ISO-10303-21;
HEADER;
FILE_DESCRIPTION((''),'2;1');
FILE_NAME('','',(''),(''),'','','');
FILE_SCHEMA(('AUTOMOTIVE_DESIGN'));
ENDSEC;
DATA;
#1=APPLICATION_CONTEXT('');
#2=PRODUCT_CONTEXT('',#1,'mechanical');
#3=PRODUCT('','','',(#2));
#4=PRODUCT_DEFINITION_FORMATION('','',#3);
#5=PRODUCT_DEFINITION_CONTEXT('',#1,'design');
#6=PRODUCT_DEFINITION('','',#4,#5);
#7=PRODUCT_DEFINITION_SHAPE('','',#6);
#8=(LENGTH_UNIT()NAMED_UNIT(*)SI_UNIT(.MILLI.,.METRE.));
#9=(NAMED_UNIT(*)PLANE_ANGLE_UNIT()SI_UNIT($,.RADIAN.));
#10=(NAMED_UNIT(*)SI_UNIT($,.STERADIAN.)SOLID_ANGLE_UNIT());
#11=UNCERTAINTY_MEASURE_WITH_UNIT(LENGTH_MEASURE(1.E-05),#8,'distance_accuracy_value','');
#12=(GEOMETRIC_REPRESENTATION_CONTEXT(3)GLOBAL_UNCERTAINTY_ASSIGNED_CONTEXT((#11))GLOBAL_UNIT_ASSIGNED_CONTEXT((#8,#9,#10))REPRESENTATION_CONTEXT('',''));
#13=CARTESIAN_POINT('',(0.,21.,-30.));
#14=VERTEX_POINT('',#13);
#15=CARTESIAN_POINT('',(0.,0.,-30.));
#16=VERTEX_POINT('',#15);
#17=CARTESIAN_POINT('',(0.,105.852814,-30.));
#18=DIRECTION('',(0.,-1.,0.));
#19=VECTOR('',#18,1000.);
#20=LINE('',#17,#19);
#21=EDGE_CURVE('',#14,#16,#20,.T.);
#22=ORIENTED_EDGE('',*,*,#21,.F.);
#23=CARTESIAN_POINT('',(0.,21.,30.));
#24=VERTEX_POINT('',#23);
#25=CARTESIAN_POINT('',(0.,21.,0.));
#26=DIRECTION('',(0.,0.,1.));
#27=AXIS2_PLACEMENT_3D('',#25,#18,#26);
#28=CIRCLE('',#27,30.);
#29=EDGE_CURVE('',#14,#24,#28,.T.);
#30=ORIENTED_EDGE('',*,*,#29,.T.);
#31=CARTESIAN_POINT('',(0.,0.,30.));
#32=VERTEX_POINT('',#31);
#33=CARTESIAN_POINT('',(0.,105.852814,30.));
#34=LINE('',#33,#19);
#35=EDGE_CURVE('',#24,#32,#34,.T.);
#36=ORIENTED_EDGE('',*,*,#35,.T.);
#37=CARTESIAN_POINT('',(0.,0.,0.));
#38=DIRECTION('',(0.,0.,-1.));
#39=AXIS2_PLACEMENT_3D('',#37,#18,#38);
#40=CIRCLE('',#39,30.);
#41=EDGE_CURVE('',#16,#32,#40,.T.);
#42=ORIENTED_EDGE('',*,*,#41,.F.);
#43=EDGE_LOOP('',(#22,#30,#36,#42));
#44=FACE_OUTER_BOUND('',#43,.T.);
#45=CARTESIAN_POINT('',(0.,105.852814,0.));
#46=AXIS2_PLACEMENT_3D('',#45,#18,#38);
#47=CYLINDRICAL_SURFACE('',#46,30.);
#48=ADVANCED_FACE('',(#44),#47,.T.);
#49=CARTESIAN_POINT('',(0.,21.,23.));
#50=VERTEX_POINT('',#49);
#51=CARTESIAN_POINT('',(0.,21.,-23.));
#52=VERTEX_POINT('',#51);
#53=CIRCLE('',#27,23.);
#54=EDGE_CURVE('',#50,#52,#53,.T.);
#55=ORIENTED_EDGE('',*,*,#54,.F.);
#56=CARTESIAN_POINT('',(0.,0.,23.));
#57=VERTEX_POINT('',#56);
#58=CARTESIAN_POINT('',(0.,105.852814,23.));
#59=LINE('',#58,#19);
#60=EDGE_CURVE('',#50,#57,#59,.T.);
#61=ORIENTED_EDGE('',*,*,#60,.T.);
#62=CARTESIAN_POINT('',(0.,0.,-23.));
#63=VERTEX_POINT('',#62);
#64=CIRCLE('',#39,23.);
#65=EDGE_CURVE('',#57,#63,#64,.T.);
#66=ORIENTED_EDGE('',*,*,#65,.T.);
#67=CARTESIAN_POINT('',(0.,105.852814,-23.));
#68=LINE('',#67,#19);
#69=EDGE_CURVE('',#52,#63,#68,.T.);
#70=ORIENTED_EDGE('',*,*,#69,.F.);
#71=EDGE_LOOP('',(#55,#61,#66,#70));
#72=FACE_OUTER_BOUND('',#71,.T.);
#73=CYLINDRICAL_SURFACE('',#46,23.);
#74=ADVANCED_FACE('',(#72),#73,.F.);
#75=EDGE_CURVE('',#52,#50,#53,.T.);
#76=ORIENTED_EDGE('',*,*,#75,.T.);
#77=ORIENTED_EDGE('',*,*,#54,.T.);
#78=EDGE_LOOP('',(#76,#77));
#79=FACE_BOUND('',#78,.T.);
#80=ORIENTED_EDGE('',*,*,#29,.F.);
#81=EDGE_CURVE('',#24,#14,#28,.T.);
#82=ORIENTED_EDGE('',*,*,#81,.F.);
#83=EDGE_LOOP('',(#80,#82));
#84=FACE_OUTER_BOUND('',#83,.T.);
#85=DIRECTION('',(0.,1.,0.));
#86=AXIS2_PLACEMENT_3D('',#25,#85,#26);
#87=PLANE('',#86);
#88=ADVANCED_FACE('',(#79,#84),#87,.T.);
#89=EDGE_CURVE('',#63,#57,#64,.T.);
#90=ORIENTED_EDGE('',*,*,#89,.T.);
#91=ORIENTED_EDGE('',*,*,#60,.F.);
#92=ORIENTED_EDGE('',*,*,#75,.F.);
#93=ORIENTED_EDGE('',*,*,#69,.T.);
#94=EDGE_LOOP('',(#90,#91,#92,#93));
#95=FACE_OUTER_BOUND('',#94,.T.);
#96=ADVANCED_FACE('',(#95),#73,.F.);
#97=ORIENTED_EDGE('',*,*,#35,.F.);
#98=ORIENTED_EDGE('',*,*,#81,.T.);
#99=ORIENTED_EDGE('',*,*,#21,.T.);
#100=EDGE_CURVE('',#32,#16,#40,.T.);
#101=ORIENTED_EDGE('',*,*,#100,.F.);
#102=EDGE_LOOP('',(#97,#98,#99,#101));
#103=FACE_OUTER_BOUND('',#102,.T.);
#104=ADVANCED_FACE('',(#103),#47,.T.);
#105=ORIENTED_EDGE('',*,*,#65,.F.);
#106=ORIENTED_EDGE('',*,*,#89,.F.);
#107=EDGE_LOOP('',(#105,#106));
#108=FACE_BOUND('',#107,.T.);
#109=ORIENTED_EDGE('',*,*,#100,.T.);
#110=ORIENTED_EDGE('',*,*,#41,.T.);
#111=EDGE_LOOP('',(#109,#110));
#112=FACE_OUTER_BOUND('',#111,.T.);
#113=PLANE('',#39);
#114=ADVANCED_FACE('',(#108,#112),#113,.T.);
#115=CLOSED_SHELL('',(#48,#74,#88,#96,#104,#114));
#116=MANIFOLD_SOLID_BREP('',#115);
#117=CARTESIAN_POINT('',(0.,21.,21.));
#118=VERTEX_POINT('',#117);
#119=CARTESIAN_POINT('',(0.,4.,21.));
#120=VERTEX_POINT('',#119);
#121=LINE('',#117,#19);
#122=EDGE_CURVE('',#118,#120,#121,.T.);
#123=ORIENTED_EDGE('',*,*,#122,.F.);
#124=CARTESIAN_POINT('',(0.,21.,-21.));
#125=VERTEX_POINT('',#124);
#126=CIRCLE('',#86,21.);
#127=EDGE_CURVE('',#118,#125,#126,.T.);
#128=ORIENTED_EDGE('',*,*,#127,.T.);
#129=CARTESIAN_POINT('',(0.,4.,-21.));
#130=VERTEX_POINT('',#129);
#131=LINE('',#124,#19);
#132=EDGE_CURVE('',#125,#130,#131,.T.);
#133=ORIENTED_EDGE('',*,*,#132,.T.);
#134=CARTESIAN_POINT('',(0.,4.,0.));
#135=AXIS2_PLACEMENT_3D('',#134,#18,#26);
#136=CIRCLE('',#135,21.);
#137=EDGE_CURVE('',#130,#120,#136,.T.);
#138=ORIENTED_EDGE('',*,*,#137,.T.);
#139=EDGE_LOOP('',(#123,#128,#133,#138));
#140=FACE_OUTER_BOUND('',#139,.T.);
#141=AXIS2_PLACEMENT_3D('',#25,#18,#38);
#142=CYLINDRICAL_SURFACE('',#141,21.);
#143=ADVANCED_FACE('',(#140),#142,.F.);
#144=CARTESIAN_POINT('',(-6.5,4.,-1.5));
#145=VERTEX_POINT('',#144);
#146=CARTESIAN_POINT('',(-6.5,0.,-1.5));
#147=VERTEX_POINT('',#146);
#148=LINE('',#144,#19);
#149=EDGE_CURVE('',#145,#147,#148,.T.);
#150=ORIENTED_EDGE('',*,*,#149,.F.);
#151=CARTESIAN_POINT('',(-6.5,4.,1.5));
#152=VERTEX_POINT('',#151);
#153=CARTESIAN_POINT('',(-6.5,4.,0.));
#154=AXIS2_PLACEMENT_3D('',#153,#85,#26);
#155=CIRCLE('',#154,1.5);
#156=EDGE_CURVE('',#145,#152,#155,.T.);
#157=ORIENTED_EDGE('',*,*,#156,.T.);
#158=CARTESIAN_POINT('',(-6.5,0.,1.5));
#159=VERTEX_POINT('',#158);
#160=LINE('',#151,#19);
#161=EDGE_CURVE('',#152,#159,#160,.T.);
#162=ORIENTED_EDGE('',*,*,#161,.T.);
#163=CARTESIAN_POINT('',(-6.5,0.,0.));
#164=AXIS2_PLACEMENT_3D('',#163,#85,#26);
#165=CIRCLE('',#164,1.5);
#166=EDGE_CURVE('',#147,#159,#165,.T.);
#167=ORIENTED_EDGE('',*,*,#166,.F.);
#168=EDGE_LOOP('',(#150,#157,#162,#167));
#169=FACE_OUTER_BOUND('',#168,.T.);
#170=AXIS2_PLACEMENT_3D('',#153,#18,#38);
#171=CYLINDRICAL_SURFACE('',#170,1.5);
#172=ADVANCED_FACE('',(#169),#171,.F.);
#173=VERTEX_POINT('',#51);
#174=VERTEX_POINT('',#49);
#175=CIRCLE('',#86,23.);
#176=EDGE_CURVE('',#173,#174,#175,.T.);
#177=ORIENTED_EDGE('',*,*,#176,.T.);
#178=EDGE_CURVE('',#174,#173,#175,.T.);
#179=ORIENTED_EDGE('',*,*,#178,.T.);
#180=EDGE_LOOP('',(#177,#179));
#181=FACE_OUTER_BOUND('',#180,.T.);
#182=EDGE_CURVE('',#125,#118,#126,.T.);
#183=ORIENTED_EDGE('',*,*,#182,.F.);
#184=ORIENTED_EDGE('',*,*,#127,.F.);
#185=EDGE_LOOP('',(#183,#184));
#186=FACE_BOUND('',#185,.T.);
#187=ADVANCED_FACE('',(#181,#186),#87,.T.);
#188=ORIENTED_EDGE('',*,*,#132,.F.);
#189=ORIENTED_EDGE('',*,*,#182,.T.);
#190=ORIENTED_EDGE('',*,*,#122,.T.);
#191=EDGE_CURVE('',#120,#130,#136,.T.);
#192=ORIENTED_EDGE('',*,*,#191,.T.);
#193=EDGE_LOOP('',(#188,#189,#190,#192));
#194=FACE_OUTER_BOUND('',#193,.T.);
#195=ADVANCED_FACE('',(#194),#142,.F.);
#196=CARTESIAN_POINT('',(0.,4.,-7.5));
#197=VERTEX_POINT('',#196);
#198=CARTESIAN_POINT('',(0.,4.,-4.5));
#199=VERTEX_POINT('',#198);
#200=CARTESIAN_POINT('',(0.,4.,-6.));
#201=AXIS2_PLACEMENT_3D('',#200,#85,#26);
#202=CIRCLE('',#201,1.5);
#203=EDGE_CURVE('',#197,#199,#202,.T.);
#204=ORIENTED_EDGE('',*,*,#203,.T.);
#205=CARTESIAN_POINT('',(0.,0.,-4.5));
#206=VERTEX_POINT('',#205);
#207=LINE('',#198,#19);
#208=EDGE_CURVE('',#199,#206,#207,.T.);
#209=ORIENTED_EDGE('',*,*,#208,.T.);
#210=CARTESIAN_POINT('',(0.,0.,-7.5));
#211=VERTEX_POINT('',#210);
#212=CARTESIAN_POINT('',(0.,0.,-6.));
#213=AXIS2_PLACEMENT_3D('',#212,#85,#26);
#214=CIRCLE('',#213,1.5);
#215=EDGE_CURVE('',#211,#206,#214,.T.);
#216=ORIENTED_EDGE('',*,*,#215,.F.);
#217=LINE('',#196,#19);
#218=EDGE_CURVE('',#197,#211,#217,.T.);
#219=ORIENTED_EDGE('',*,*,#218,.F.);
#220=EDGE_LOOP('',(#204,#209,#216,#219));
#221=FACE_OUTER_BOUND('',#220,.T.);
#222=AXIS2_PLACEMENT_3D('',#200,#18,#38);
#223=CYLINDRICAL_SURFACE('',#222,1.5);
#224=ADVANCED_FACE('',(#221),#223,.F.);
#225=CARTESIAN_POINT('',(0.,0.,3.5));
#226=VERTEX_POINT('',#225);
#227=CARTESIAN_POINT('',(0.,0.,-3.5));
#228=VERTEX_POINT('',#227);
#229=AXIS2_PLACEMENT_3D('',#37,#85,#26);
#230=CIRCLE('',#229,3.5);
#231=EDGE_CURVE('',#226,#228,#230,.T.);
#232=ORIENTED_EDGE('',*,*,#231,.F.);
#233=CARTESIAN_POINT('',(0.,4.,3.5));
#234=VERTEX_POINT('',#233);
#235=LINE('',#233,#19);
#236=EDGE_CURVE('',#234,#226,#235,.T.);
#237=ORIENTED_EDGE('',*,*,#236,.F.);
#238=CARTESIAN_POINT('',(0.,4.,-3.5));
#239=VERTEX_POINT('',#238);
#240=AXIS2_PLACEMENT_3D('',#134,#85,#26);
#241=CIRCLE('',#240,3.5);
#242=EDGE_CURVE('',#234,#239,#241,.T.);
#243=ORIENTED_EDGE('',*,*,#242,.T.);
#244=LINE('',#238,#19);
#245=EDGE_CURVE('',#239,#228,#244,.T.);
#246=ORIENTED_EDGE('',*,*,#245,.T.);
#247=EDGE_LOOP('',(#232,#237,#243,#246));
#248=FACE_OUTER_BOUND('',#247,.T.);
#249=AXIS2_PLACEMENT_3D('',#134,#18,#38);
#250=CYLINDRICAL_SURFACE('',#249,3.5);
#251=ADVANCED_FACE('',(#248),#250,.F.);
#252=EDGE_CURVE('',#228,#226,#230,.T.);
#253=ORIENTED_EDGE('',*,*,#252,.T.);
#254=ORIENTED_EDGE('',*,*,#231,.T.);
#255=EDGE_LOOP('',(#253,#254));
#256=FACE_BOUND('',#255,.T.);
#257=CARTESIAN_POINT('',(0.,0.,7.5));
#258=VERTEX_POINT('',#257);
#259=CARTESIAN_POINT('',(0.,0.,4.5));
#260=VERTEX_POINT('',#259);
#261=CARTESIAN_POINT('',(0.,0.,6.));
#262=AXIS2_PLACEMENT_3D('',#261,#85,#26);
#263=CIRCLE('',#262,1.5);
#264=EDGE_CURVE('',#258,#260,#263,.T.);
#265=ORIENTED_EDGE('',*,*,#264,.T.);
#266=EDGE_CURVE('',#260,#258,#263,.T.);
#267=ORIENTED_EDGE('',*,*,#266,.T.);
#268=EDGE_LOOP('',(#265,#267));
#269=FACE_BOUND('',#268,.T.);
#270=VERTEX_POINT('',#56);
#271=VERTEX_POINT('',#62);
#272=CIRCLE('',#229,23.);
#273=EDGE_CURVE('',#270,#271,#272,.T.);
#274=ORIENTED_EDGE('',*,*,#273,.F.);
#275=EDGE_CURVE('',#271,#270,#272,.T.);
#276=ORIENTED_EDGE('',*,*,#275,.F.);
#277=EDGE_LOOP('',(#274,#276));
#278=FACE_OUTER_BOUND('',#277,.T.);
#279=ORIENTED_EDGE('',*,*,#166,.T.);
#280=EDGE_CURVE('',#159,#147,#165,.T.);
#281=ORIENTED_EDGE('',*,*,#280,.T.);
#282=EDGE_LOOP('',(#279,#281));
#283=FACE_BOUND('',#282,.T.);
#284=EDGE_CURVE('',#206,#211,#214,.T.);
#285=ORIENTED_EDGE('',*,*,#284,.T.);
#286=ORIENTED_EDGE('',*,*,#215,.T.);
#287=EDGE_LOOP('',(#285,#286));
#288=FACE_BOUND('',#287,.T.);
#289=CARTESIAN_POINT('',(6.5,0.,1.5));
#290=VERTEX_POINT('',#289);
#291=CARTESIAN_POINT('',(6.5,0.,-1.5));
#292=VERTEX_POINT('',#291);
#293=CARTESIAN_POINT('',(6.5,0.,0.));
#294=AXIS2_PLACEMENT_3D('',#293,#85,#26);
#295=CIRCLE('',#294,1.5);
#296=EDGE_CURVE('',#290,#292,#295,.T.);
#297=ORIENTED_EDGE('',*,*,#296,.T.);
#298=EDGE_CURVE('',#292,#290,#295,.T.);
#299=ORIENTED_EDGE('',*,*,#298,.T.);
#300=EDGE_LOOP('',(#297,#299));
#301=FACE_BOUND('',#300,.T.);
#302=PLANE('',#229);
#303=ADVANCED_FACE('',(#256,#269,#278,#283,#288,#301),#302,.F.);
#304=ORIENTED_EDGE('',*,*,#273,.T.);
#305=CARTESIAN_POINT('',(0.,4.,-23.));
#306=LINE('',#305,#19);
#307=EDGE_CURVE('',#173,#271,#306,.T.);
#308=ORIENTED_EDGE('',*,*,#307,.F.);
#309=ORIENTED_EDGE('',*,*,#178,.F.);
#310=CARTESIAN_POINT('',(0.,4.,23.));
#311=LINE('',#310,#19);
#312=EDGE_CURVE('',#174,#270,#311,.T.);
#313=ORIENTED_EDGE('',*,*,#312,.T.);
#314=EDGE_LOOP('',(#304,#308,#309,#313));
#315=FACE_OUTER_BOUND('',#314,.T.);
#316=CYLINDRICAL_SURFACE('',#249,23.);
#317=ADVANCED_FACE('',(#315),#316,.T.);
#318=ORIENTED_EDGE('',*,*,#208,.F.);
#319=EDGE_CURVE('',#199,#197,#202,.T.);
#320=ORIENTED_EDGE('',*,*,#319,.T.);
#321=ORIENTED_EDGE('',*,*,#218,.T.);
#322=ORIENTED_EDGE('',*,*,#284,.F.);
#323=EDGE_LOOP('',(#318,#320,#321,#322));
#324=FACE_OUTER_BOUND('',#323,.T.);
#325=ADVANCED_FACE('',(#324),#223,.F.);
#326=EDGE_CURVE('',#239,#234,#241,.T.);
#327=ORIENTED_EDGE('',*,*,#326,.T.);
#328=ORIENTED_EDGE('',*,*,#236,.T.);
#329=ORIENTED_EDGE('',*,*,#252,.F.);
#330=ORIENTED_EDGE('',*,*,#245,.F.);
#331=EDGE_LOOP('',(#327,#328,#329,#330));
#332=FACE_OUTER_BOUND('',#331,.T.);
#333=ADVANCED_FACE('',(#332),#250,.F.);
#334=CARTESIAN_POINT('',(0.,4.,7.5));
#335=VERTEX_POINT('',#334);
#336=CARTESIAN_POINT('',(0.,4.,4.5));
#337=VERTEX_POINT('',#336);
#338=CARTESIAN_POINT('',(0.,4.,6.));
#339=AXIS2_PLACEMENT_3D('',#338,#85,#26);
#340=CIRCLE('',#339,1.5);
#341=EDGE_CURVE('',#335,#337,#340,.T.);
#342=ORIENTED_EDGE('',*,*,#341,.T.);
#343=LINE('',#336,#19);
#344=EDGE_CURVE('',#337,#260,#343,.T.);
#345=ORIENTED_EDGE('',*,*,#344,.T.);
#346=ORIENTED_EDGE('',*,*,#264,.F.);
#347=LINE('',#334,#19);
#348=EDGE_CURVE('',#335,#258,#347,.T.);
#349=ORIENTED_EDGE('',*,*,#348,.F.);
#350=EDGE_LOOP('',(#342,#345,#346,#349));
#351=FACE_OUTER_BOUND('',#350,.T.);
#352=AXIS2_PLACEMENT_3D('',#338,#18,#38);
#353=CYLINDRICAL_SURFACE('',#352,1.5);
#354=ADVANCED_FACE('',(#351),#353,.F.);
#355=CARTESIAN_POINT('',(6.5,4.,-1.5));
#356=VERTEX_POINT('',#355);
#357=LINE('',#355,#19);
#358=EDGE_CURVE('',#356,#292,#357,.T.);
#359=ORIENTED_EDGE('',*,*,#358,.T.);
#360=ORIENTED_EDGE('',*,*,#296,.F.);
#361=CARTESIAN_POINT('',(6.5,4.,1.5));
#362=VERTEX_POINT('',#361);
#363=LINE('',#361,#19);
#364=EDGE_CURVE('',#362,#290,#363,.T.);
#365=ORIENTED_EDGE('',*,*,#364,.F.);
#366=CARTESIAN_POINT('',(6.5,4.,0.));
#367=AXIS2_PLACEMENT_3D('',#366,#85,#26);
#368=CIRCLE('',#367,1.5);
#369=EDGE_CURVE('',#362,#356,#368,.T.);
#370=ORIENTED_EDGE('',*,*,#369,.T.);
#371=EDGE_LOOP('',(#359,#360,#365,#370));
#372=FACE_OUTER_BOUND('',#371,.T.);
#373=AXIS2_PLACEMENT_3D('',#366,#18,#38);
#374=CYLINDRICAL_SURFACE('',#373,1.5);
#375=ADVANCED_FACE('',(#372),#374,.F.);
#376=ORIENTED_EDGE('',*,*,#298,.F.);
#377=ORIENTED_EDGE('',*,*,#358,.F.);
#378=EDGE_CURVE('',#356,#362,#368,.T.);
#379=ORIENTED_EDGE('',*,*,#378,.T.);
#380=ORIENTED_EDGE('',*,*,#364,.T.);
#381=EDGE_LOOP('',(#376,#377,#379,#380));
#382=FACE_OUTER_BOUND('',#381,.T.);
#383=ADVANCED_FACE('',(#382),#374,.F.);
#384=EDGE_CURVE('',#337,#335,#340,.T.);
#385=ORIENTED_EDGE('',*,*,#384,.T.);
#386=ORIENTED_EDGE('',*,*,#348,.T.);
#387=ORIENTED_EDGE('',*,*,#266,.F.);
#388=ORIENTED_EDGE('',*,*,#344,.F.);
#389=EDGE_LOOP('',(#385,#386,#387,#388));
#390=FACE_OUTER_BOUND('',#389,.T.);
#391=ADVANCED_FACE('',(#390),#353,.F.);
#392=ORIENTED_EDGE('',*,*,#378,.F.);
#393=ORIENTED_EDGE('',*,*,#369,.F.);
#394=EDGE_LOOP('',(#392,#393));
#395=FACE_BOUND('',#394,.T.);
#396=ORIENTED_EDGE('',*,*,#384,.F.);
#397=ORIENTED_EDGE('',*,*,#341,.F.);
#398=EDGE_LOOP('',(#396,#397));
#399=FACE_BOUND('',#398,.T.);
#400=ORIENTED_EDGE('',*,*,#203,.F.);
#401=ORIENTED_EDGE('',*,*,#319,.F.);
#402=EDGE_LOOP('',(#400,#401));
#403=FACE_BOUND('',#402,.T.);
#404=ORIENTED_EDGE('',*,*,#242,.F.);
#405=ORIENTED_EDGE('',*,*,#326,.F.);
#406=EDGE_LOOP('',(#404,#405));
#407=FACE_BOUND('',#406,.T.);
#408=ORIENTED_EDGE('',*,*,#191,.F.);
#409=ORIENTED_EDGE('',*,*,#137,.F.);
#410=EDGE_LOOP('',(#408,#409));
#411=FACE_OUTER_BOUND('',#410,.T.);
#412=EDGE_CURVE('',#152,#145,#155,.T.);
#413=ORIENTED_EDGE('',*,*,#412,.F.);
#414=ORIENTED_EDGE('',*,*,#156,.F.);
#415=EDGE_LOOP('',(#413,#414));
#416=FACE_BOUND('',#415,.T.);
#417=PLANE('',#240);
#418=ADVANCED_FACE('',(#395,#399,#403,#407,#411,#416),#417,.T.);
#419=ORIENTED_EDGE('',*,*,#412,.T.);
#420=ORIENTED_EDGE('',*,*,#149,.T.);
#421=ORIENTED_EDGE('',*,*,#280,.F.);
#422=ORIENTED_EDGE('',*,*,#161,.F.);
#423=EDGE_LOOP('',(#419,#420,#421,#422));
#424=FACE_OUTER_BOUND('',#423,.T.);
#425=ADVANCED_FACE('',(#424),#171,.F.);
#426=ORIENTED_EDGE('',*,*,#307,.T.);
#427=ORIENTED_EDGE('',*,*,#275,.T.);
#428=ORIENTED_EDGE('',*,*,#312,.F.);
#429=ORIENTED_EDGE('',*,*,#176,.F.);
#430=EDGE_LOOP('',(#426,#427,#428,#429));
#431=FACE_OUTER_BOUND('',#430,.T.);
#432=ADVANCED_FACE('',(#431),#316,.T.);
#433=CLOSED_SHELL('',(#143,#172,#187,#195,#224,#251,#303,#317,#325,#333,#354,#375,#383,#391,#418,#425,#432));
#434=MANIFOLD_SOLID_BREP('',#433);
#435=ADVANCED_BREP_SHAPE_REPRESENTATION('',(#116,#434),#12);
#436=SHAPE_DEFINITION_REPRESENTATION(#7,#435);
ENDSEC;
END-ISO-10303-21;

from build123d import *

# Parameters (mm, degrees)
SKETCH1_R           = 23
SKETCH1_R_2         = 1.5
SKETCH1_R_3         = 3.5
BOSS_EXTRUDE1_DEPTH = 4
SKETCH2_R           = 23
SKETCH2_R_2         = 21
BOSS_EXTRUDE2_DEPTH = 17
SKETCH3_R           = 30
SKETCH3_R_2         = 23
BOSS_EXTRUDE3_DEPTH = 21


with BuildPart() as part:
    # Sketch1 → Boss-Extrude1 (new body)
    with BuildSketch(Plane(origin=(0, 0, 0), x_dir=(1, 0, 0), z_dir=(0, 1, 0))):
        with Locations(Location((0, 0, 0), (0, 0, 270))):
            Circle(SKETCH1_R)
        with Locations(Location((6.5, 0, 0), (0, 0, 270))):
            Circle(SKETCH1_R_2, mode=Mode.SUBTRACT)
        with Locations(Location((-6.5, 0, 0), (0, 0, 270))):
            Circle(SKETCH1_R_2, mode=Mode.SUBTRACT)
        with Locations(Location((0, -6, 0), (0, 0, 270))):
            Circle(SKETCH1_R_2, mode=Mode.SUBTRACT)
        with Locations(Location((0, 6, 0), (0, 0, 270))):
            Circle(SKETCH1_R_2, mode=Mode.SUBTRACT)
        with Locations(Location((0, 0, 0), (0, 0, 270))):
            Circle(SKETCH1_R_3, mode=Mode.SUBTRACT)
    extrude(amount=BOSS_EXTRUDE1_DEPTH)

    # Sketch2 → Boss-Extrude2 (add)
    with BuildSketch(Plane(origin=(0, 4, 0), x_dir=(1, 0, 0), z_dir=(0, 1, 0))):
        with Locations(Location((0, 0, 0), (0, 0, 270))):
            Circle(SKETCH2_R)
        with Locations(Location((0, 0, 0), (0, 0, 270))):
            Circle(SKETCH2_R_2, mode=Mode.SUBTRACT)
    extrude(amount=BOSS_EXTRUDE2_DEPTH)


with BuildPart() as body_2:
    # Sketch3 → Boss-Extrude3 (new body)
    with BuildSketch(Plane.XZ):
        with Locations(Location((0, 0, 0), (0, 0, 270))):
            Circle(SKETCH3_R)
        with Locations(Location((0, 0, 0), (0, 0, 270))):
            Circle(SKETCH3_R_2, mode=Mode.SUBTRACT)
    extrude(amount=-BOSS_EXTRUDE3_DEPTH)


solid = Compound([part.part, body_2.part])
